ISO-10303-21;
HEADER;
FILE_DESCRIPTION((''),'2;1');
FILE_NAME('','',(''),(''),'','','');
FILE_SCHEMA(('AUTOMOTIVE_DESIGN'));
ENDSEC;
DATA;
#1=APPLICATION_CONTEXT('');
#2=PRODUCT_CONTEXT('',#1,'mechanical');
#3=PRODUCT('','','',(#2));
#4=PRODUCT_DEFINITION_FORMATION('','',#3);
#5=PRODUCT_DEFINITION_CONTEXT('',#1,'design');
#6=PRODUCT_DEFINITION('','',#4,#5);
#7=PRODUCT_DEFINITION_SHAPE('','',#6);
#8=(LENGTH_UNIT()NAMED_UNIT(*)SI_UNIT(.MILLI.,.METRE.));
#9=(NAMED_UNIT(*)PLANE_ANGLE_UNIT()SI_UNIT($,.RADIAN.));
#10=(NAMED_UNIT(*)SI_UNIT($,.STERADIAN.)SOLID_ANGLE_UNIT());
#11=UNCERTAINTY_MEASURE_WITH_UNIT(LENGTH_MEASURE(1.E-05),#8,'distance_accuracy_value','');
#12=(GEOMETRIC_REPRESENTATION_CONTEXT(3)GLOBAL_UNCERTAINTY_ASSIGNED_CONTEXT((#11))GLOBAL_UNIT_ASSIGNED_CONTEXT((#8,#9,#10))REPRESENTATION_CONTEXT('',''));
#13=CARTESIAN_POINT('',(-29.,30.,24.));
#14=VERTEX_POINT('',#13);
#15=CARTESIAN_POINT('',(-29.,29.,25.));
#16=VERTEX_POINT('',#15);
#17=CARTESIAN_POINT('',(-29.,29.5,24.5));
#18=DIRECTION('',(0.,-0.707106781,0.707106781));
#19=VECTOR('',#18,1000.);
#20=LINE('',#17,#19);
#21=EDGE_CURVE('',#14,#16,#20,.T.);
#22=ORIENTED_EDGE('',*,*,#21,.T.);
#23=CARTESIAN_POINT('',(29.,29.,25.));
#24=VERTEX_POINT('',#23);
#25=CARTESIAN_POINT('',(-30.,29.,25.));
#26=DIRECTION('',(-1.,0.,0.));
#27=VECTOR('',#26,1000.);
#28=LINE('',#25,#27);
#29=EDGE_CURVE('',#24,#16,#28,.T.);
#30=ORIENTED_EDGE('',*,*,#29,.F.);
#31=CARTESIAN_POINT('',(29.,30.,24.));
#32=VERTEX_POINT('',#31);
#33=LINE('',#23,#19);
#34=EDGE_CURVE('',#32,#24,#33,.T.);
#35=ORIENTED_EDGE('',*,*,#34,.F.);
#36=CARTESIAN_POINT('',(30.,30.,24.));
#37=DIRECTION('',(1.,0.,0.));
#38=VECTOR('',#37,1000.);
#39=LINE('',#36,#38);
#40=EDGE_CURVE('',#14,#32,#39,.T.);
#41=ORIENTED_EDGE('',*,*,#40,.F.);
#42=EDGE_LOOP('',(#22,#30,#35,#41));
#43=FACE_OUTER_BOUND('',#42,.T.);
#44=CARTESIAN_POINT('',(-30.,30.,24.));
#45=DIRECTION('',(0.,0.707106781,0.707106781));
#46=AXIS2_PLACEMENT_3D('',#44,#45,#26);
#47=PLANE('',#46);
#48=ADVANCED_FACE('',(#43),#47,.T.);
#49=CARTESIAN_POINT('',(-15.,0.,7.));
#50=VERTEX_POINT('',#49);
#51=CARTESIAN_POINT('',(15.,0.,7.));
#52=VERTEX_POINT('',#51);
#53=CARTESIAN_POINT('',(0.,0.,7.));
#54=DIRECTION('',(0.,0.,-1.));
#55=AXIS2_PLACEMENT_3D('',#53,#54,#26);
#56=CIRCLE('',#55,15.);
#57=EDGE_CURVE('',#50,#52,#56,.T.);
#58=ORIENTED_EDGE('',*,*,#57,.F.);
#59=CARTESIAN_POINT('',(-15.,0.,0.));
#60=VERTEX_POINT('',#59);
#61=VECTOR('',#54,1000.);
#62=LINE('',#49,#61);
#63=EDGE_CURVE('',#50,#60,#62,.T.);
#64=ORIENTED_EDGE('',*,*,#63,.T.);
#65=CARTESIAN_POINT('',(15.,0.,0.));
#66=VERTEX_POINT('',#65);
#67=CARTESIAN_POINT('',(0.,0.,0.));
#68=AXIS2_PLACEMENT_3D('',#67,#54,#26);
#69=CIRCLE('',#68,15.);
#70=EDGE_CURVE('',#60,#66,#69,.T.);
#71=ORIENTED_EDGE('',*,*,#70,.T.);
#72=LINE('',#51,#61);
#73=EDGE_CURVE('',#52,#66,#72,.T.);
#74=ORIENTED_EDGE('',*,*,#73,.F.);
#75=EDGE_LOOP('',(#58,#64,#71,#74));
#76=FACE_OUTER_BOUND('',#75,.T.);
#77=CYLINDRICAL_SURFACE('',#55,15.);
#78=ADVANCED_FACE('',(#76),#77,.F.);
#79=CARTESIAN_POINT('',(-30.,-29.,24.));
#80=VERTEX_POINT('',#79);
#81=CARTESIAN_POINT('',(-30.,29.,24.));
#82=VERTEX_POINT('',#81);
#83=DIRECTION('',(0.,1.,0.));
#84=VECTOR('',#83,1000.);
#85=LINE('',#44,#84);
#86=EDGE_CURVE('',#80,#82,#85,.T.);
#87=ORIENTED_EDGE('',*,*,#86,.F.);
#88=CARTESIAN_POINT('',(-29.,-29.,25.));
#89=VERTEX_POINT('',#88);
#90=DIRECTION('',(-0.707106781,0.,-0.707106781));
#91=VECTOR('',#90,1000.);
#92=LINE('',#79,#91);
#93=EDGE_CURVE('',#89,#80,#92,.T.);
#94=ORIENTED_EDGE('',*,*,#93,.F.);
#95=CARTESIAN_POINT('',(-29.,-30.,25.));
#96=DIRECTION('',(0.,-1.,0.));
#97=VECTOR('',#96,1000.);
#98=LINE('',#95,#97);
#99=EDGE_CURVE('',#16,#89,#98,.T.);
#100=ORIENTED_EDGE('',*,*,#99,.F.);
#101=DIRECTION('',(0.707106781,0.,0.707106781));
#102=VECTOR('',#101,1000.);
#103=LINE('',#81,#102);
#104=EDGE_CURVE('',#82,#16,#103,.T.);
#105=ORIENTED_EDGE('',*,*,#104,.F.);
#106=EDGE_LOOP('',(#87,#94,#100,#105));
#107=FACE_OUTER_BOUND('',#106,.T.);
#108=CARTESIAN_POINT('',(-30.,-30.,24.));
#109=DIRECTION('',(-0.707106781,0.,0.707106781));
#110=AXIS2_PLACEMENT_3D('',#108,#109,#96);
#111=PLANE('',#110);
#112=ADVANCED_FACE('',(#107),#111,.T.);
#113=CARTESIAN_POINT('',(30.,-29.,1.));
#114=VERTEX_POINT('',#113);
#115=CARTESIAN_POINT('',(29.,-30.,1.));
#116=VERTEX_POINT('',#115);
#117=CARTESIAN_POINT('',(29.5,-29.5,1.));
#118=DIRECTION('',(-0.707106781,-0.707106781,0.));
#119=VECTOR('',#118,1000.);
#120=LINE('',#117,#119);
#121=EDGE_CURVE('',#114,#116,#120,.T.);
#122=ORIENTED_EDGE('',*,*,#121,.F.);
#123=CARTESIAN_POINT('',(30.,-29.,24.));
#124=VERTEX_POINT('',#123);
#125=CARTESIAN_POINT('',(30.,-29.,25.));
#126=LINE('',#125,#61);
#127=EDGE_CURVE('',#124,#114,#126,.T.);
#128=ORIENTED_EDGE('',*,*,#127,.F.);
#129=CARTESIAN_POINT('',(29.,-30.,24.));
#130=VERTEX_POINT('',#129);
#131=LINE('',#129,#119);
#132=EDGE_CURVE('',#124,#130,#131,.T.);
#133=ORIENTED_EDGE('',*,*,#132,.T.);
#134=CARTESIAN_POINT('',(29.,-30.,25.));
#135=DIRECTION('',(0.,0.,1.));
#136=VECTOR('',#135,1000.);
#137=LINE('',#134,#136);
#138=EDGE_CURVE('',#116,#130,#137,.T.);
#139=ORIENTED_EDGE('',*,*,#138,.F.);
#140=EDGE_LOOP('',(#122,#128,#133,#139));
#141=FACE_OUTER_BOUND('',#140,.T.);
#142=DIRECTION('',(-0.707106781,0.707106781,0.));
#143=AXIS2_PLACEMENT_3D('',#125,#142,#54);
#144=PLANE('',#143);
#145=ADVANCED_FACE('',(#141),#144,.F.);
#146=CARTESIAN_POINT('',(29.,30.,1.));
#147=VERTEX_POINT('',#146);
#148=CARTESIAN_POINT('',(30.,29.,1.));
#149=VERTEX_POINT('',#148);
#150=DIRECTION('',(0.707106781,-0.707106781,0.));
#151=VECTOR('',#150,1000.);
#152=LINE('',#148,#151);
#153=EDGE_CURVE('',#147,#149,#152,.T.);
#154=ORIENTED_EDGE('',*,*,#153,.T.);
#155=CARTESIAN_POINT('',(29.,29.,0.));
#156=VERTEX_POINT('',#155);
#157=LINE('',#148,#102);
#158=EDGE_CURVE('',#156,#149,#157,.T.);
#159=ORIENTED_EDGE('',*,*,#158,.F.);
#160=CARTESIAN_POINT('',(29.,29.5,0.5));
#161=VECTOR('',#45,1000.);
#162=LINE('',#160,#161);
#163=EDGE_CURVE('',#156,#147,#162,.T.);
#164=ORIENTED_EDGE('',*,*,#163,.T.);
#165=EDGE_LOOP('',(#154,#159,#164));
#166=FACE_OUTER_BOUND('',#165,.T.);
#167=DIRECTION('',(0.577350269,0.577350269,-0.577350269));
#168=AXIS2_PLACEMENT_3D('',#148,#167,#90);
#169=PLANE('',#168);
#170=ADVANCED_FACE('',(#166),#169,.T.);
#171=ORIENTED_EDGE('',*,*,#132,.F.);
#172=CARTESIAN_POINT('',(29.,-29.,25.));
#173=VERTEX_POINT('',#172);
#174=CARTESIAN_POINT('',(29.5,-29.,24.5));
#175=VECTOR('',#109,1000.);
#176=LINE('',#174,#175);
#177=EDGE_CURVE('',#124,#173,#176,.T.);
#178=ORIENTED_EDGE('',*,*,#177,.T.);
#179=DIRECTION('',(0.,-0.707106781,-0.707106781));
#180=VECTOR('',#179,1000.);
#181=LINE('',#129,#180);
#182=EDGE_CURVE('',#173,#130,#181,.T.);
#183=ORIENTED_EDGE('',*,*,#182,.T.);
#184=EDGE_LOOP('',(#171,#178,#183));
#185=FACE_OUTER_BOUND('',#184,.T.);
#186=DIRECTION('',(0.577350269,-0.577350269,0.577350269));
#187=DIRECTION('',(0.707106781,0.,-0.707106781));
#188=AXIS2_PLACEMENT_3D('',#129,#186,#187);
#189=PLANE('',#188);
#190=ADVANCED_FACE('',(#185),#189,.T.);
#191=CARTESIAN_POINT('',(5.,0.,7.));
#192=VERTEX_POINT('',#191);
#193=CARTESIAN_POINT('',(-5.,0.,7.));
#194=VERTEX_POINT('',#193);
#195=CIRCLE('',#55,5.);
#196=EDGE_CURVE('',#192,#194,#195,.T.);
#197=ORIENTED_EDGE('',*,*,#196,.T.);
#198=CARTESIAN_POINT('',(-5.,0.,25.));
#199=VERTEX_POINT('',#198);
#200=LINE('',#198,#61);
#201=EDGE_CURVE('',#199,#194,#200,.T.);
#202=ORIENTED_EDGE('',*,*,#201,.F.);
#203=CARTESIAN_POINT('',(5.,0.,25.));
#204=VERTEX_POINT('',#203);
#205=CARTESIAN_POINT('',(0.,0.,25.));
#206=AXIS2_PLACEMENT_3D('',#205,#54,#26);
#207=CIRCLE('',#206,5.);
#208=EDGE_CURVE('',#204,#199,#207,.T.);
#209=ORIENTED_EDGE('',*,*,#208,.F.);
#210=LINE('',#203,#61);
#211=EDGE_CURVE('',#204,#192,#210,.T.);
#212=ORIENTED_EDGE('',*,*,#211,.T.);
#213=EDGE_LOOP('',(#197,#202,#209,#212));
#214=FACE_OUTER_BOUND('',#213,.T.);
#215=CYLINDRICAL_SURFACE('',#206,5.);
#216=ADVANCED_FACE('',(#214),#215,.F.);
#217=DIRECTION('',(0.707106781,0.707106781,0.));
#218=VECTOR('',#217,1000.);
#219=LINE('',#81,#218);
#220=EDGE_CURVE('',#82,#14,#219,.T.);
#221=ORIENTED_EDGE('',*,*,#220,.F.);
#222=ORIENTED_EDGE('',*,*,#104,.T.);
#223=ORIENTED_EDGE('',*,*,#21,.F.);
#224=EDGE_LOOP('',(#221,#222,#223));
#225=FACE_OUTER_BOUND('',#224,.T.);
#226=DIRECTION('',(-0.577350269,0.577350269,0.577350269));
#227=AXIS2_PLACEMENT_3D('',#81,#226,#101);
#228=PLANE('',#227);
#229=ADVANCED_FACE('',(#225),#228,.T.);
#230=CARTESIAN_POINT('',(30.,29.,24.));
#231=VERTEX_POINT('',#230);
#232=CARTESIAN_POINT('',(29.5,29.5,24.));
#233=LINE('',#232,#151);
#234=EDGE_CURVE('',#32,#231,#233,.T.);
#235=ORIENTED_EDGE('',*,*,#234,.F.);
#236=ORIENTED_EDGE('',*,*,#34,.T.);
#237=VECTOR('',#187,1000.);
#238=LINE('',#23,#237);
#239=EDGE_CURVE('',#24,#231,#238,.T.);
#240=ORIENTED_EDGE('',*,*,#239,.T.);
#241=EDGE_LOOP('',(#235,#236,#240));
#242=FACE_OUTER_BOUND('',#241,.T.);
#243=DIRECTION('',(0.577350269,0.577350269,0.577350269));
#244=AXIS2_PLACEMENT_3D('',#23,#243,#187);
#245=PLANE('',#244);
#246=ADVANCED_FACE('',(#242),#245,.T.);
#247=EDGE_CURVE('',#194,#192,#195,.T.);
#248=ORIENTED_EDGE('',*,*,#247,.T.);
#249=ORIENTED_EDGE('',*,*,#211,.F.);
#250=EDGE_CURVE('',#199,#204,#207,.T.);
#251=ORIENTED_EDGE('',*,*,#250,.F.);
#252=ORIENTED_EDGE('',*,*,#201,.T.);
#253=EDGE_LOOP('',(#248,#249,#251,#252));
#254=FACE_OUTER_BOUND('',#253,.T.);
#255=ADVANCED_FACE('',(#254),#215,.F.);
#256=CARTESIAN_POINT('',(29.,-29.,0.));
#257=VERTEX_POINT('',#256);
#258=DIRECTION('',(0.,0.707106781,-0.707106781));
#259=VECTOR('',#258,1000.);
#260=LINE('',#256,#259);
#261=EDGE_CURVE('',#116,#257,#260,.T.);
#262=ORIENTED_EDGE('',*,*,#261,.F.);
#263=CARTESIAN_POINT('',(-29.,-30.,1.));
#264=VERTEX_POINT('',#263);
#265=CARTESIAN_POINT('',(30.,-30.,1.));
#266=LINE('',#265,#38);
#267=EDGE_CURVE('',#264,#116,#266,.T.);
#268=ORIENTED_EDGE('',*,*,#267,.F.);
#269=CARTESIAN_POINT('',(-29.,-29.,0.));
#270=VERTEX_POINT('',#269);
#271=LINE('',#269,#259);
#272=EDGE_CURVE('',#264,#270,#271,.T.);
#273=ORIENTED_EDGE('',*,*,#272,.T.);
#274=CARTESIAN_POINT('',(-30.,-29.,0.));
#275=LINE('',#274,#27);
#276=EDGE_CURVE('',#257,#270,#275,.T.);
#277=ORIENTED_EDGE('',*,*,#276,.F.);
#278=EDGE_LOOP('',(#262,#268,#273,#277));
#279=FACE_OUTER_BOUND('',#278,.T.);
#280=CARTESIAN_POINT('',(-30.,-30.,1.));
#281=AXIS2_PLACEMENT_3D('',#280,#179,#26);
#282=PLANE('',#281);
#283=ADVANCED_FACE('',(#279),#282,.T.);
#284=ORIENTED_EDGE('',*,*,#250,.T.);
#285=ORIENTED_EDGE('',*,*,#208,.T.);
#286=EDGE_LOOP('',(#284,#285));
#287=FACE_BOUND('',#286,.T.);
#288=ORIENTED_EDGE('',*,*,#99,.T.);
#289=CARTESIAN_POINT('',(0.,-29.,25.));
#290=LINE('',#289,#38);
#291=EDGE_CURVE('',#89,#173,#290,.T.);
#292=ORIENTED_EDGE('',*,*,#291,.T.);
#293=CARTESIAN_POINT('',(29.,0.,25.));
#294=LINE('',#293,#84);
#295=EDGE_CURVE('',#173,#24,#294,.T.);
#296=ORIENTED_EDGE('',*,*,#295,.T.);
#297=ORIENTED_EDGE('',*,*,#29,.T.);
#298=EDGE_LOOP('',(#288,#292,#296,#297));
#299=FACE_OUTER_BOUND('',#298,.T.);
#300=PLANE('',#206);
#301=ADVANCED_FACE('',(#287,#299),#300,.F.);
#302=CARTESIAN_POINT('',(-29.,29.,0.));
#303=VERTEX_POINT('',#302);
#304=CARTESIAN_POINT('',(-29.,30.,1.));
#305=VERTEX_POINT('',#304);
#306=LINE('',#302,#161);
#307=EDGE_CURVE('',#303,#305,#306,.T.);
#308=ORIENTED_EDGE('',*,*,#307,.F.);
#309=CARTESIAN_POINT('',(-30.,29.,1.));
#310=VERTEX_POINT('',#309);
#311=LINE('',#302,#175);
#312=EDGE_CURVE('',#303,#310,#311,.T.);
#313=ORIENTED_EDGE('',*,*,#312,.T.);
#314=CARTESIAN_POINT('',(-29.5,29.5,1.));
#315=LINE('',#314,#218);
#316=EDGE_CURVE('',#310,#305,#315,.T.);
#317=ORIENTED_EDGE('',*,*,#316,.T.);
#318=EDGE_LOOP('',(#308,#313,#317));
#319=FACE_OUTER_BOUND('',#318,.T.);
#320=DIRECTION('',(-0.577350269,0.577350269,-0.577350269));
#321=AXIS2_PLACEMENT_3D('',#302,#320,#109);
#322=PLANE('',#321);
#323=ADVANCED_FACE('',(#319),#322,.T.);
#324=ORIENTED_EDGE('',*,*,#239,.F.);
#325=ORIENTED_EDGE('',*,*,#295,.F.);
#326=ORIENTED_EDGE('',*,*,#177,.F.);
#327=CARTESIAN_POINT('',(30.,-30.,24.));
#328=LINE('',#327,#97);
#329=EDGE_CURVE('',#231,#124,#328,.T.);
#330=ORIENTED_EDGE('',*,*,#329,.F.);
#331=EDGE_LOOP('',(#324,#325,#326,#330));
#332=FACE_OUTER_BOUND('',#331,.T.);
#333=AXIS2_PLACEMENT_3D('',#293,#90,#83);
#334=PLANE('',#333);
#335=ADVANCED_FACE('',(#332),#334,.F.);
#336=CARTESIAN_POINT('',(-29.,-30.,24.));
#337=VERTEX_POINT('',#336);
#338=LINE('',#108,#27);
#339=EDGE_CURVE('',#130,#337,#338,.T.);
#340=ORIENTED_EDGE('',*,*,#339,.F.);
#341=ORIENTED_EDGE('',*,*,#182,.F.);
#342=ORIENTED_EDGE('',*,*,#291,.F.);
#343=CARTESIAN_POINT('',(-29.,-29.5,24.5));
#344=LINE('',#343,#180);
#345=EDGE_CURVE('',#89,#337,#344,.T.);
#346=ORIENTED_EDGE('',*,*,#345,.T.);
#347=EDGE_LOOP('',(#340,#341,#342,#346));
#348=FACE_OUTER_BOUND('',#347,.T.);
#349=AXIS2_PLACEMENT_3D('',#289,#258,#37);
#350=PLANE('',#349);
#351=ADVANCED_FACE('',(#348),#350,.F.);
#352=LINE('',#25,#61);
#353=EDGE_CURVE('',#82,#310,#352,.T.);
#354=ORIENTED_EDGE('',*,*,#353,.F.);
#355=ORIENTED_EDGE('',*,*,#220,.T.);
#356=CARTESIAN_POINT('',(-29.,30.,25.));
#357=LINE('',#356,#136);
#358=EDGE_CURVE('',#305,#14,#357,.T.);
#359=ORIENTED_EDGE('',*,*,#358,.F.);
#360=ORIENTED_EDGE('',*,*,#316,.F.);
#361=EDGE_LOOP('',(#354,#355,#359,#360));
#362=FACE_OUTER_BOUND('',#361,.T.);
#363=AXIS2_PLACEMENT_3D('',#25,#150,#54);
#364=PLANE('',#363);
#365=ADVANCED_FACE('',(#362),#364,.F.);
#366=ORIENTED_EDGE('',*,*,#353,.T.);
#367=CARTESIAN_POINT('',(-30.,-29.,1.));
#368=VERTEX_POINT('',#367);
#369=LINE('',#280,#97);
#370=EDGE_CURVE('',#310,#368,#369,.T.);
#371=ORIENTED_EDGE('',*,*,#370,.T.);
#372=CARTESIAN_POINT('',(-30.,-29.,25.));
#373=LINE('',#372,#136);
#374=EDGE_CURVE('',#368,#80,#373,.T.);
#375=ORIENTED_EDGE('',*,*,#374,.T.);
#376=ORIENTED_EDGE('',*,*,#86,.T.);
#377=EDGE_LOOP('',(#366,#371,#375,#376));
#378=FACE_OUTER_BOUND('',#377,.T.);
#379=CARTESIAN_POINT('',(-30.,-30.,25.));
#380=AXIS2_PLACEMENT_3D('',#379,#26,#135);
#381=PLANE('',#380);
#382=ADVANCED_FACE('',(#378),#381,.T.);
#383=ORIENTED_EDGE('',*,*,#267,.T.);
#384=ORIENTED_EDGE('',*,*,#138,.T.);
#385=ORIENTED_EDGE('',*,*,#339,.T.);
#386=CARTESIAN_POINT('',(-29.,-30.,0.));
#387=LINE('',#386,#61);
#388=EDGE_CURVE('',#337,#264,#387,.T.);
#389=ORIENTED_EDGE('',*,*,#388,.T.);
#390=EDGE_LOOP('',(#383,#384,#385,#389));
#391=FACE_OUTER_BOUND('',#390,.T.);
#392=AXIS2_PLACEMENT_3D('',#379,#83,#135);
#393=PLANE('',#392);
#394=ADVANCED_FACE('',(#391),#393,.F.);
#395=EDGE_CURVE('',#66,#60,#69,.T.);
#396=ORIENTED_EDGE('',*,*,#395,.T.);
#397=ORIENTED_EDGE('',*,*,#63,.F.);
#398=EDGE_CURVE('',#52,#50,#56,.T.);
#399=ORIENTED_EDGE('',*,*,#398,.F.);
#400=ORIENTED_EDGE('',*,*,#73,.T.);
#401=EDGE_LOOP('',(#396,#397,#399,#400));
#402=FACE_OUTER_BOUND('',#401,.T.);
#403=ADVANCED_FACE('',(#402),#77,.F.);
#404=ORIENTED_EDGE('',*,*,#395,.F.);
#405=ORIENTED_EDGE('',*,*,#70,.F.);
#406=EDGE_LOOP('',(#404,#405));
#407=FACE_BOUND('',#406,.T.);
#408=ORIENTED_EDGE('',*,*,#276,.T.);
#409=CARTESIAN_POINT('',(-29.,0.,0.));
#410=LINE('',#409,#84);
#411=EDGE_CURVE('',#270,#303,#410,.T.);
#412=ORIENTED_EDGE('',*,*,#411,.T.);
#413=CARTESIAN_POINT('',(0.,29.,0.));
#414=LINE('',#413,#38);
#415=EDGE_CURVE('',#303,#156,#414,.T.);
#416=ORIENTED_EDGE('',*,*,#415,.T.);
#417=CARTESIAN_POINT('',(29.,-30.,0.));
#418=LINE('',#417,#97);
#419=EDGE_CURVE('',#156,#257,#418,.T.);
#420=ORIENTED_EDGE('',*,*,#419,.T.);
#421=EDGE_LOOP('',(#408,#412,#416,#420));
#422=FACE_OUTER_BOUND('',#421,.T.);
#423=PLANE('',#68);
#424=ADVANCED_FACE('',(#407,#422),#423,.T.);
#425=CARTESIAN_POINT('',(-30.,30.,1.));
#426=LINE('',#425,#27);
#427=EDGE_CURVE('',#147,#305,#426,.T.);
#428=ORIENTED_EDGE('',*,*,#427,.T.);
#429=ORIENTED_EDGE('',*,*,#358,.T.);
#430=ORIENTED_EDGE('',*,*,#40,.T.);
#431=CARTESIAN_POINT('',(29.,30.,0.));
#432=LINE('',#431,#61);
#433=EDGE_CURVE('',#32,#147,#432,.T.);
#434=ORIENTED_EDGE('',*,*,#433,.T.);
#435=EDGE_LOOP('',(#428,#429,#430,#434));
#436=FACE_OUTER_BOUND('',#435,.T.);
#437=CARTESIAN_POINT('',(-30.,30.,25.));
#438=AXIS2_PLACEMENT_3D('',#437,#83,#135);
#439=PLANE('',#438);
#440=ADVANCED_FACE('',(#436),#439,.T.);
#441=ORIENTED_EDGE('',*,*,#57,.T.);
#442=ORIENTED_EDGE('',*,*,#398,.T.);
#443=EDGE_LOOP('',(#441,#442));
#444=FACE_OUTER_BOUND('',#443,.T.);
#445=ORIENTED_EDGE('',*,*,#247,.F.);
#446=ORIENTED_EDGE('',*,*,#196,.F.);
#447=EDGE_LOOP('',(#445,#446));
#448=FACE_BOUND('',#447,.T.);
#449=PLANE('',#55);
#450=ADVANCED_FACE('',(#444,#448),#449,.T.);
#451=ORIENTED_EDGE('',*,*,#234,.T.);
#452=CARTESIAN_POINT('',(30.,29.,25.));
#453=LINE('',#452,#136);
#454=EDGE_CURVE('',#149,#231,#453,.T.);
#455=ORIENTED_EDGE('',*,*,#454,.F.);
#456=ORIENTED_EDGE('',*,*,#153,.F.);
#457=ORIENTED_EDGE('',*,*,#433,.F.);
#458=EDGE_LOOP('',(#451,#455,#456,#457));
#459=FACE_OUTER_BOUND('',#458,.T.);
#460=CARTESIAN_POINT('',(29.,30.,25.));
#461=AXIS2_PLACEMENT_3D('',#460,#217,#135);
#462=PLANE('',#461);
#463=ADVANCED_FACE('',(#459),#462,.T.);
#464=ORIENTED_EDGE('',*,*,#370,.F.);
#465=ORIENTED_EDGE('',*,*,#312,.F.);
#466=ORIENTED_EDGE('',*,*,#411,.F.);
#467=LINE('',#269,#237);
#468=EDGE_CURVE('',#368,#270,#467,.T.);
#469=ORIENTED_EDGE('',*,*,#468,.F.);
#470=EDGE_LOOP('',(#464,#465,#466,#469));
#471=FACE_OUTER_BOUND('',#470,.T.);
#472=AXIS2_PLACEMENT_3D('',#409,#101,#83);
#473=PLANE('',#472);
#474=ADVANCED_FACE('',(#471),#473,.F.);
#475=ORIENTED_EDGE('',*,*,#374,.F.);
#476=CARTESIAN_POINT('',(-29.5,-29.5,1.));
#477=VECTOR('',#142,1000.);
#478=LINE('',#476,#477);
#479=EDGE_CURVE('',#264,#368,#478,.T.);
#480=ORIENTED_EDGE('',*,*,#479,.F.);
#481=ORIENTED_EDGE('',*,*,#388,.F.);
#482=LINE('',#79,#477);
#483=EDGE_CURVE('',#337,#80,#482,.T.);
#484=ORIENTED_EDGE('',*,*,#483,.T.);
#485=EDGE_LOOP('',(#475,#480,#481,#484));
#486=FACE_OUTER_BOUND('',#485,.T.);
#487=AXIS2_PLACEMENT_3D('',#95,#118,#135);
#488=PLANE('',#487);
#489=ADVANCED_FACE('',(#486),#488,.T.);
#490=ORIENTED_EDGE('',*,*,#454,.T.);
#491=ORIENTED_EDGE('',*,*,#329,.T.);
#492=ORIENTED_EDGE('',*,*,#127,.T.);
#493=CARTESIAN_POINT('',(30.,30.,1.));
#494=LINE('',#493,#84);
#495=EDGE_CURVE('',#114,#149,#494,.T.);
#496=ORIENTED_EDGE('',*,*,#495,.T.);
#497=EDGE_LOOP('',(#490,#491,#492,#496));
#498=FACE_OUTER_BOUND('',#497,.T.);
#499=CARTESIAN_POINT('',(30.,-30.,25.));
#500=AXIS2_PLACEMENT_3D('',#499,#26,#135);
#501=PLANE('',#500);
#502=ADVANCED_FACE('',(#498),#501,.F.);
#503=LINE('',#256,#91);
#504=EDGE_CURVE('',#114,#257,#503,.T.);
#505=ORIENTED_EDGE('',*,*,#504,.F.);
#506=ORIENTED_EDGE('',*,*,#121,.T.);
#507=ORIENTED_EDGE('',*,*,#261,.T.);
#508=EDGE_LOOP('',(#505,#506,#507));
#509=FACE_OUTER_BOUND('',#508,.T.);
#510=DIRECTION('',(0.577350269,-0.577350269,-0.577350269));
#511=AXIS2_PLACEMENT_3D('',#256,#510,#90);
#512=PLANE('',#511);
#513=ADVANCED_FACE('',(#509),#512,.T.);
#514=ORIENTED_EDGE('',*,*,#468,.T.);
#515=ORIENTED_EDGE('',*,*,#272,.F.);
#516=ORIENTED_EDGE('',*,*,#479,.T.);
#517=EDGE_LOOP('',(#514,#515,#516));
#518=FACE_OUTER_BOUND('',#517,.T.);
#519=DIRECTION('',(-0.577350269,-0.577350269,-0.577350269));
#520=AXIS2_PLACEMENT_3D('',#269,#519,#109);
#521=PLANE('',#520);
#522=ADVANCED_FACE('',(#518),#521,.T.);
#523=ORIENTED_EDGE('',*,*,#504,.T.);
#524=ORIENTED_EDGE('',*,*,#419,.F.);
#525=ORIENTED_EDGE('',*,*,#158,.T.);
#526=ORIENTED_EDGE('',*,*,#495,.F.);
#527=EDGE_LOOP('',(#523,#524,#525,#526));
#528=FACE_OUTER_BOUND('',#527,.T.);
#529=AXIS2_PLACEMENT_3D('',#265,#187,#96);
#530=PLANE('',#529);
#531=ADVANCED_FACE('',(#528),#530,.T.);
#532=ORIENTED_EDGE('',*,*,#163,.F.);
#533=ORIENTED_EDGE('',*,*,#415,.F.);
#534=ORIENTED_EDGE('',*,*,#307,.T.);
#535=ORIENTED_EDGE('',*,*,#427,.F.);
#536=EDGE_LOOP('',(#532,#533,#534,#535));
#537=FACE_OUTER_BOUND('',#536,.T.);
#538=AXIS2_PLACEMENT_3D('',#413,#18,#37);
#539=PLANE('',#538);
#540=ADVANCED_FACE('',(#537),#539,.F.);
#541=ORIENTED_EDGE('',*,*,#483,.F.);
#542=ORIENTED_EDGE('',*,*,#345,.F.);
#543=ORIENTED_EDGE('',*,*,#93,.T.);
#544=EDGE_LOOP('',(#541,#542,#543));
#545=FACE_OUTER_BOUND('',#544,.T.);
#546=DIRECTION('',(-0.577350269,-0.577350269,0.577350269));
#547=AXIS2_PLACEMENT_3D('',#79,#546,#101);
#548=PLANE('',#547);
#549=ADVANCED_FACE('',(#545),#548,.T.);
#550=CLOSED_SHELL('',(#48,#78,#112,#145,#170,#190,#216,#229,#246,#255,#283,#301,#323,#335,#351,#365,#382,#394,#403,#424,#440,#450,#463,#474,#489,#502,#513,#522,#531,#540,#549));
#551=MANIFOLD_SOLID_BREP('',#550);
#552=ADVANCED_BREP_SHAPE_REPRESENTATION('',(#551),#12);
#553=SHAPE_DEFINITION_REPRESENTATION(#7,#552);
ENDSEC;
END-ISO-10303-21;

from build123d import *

# Parameters (mm, degrees)
SKETCH1_W           = 60
SKETCH1_H           = 60
BOSS_EXTRUDE1_DEPTH = 25
CHAMFER1_SIZE       = 1
SKETCH2_R           = 15
CUT_EXTRUDE1_DEPTH  = 7
SKETCH3_R           = 5
CUT_EXTRUDE2_DEPTH  = 47.086874487


with BuildPart() as part:
    # Sketch1 → Boss-Extrude1 (new body)
    with BuildSketch(Plane.XY):
        Rectangle(SKETCH1_W, SKETCH1_H)
    extrude(amount=BOSS_EXTRUDE1_DEPTH)

    # Chamfer1
    chamfer1_edges = [part.edges().sort_by_distance(p)[0] for p in [
        (30, 0, 25),
        (0, -30, 25),
        (-30, 0, 25),
        (0, -30, 0),
        (30, 0, 0),
        (0, 30, 0),
        (-30, 0, 0),
        (0, 30, 25),
        (-30, -30, 12.5),
        (30, -30, 12.5),
        (30, 30, 12.5),
        (-30, 30, 12.5),
    ]]
    chamfer(chamfer1_edges, length=CHAMFER1_SIZE)

    # Sketch2 → Cut-Extrude1 (cut)
    with BuildSketch(Plane(origin=(0, 0, 0), x_dir=(-1, 0, 0), z_dir=(0, 0, -1))):
        Circle(SKETCH2_R)
    extrude(amount=-CUT_EXTRUDE1_DEPTH, mode=Mode.SUBTRACT)

    # Sketch3 → Cut-Extrude2 (cut, through all)
    with BuildSketch(Plane(origin=(0, 0, 7), x_dir=(-1, 0, 0), z_dir=(0, 0, -1))):
        Circle(SKETCH3_R)
    extrude(amount=-CUT_EXTRUDE2_DEPTH, mode=Mode.SUBTRACT)


solid = part.part
